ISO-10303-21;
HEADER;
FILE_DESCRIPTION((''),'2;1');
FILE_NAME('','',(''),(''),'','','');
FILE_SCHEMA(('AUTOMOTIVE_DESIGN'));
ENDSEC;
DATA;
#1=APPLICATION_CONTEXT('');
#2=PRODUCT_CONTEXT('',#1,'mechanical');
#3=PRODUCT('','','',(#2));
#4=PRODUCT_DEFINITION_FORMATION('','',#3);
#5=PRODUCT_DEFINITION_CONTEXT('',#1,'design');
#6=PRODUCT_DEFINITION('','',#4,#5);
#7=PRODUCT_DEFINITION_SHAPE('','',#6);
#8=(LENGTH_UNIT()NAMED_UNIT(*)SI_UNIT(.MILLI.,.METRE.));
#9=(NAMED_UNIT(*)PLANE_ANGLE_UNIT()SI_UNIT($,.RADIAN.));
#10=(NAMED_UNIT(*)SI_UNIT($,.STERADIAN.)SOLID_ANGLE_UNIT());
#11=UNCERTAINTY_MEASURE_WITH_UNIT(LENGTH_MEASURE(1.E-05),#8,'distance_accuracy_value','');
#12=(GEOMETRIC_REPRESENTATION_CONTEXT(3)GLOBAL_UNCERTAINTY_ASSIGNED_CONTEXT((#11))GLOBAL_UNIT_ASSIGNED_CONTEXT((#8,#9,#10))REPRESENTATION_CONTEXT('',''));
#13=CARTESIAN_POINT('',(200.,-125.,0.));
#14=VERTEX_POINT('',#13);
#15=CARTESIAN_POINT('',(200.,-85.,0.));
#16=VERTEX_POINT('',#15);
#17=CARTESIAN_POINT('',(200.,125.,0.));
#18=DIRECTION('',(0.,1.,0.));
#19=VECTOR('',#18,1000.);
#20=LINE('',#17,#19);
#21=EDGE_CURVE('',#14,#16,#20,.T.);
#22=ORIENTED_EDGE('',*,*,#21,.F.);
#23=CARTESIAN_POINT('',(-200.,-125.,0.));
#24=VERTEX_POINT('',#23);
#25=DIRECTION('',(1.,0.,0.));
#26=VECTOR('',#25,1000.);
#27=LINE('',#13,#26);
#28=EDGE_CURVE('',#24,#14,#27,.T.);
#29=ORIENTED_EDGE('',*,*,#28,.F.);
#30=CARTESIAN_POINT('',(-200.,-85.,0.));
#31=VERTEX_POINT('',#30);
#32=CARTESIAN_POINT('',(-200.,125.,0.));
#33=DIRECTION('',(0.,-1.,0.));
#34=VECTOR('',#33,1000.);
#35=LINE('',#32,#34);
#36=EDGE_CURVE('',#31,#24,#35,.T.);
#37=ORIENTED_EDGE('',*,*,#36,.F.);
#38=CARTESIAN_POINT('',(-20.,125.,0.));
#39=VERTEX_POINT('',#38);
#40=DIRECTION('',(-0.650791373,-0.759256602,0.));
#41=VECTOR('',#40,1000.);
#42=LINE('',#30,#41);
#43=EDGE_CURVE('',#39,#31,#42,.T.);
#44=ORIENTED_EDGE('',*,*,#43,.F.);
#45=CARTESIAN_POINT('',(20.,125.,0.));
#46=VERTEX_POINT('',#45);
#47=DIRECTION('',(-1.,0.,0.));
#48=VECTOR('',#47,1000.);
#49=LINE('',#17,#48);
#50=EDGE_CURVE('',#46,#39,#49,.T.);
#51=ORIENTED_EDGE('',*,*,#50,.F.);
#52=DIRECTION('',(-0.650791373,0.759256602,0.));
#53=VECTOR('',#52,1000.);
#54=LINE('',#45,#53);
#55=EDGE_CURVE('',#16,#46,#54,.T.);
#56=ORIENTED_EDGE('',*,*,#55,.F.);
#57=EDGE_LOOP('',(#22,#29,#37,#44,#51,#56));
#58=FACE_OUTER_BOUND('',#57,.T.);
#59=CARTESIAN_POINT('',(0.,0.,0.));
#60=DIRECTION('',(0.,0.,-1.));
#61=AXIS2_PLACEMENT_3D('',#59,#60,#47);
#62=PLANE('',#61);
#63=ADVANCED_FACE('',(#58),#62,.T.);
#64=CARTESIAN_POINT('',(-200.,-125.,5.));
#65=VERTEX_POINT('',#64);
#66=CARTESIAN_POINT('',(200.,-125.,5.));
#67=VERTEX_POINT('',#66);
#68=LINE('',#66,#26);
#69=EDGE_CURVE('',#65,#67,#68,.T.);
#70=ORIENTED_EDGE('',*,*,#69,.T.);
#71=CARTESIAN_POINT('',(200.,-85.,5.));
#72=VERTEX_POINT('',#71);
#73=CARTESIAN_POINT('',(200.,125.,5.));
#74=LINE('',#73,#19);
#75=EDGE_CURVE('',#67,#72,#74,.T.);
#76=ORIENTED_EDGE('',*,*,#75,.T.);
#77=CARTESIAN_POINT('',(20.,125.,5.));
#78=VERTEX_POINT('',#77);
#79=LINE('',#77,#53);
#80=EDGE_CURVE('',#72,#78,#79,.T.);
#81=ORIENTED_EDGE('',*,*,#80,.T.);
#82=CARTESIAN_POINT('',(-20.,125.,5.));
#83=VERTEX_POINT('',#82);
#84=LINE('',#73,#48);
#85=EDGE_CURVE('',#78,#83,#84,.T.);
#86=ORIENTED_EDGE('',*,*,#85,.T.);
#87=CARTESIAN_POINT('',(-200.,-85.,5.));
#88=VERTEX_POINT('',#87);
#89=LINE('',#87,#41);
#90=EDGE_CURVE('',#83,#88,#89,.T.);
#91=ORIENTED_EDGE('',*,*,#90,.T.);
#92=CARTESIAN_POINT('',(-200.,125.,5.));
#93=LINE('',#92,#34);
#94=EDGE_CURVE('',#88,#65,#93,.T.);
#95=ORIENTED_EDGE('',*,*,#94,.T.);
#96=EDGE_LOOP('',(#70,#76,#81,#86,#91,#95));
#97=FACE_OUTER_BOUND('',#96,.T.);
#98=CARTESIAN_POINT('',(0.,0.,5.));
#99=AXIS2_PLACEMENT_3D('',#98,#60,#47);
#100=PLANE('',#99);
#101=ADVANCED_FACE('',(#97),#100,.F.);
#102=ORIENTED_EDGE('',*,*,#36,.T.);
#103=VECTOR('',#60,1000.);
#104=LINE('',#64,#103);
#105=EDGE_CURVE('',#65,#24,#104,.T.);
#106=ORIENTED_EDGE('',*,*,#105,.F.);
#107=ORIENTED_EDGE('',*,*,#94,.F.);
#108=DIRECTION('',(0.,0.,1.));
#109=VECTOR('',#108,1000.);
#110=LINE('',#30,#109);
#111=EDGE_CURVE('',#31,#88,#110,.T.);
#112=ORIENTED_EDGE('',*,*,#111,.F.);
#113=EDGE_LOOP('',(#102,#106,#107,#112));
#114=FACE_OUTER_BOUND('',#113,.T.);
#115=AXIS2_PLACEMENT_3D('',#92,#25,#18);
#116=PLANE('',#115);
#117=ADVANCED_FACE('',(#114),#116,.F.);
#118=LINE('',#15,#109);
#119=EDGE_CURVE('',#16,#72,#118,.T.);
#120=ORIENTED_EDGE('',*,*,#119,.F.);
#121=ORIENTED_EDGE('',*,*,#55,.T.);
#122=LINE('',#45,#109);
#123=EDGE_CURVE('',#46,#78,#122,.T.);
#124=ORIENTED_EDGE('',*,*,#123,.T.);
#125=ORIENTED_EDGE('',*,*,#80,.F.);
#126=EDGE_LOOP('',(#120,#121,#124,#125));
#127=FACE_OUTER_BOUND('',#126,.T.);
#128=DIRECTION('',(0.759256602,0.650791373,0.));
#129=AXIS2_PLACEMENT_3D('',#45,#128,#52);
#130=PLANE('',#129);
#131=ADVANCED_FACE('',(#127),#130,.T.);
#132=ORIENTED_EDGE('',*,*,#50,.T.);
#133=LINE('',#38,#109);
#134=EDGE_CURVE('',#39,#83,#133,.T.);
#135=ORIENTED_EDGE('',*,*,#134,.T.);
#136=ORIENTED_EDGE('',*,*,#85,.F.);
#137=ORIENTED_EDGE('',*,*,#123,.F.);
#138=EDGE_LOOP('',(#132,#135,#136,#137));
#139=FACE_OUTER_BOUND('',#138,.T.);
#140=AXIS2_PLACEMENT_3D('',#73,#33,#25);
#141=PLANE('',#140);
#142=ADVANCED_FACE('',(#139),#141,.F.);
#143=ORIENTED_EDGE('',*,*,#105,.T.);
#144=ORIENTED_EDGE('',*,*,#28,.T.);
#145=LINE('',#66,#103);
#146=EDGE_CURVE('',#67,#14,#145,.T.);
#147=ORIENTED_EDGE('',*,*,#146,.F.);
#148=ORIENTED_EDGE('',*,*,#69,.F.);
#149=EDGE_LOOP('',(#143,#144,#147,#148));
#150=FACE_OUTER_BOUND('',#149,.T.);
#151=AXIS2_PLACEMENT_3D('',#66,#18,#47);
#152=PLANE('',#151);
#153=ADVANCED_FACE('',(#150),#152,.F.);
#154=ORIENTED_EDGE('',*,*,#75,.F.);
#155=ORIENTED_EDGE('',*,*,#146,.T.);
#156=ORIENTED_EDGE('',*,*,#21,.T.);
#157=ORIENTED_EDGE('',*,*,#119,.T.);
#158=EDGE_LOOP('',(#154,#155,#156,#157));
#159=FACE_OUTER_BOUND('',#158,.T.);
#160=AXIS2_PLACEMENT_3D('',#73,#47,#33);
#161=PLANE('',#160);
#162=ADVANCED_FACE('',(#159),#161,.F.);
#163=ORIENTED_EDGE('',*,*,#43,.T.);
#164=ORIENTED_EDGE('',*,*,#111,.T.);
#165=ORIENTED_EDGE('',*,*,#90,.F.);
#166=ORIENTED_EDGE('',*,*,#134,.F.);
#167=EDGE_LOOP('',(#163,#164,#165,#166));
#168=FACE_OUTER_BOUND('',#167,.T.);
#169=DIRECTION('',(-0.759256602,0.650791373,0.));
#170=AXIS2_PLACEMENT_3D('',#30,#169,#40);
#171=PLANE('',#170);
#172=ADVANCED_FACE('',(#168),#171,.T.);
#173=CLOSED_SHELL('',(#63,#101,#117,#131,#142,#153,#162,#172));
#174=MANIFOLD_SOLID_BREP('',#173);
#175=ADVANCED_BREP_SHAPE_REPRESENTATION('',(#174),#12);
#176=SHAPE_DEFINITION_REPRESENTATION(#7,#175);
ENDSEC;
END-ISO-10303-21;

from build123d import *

# Parameters (mm, degrees)
SKETCH1_W           = 400
SKETCH1_H           = 250
BOSS_EXTRUDE1_DEPTH = 5
SKETCH2_OUTSIDE_W   = 496.346
SKETCH2_OUTSIDE_H   = 346.346
CUT_EXTRUDE1_DEPTH  = 5


with BuildPart() as part:
    # Sketch1 → Boss-Extrude1 (new body)
    with BuildSketch(Plane.XY):
        Rectangle(SKETCH1_W, SKETCH1_H)
    extrude(amount=BOSS_EXTRUDE1_DEPTH)

    # Sketch2 outside → Cut-Extrude1 (cut)
    with BuildSketch(Plane.XY.offset(5)):
        Rectangle(SKETCH2_OUTSIDE_W, SKETCH2_OUTSIDE_H)
        Polygon((-200, -85), (-20, 125), (20, 125), (200, -85), (200, -125), (-200, -125), align=None, mode=Mode.SUBTRACT)
    extrude(amount=-CUT_EXTRUDE1_DEPTH, mode=Mode.SUBTRACT)


solid = part.part
